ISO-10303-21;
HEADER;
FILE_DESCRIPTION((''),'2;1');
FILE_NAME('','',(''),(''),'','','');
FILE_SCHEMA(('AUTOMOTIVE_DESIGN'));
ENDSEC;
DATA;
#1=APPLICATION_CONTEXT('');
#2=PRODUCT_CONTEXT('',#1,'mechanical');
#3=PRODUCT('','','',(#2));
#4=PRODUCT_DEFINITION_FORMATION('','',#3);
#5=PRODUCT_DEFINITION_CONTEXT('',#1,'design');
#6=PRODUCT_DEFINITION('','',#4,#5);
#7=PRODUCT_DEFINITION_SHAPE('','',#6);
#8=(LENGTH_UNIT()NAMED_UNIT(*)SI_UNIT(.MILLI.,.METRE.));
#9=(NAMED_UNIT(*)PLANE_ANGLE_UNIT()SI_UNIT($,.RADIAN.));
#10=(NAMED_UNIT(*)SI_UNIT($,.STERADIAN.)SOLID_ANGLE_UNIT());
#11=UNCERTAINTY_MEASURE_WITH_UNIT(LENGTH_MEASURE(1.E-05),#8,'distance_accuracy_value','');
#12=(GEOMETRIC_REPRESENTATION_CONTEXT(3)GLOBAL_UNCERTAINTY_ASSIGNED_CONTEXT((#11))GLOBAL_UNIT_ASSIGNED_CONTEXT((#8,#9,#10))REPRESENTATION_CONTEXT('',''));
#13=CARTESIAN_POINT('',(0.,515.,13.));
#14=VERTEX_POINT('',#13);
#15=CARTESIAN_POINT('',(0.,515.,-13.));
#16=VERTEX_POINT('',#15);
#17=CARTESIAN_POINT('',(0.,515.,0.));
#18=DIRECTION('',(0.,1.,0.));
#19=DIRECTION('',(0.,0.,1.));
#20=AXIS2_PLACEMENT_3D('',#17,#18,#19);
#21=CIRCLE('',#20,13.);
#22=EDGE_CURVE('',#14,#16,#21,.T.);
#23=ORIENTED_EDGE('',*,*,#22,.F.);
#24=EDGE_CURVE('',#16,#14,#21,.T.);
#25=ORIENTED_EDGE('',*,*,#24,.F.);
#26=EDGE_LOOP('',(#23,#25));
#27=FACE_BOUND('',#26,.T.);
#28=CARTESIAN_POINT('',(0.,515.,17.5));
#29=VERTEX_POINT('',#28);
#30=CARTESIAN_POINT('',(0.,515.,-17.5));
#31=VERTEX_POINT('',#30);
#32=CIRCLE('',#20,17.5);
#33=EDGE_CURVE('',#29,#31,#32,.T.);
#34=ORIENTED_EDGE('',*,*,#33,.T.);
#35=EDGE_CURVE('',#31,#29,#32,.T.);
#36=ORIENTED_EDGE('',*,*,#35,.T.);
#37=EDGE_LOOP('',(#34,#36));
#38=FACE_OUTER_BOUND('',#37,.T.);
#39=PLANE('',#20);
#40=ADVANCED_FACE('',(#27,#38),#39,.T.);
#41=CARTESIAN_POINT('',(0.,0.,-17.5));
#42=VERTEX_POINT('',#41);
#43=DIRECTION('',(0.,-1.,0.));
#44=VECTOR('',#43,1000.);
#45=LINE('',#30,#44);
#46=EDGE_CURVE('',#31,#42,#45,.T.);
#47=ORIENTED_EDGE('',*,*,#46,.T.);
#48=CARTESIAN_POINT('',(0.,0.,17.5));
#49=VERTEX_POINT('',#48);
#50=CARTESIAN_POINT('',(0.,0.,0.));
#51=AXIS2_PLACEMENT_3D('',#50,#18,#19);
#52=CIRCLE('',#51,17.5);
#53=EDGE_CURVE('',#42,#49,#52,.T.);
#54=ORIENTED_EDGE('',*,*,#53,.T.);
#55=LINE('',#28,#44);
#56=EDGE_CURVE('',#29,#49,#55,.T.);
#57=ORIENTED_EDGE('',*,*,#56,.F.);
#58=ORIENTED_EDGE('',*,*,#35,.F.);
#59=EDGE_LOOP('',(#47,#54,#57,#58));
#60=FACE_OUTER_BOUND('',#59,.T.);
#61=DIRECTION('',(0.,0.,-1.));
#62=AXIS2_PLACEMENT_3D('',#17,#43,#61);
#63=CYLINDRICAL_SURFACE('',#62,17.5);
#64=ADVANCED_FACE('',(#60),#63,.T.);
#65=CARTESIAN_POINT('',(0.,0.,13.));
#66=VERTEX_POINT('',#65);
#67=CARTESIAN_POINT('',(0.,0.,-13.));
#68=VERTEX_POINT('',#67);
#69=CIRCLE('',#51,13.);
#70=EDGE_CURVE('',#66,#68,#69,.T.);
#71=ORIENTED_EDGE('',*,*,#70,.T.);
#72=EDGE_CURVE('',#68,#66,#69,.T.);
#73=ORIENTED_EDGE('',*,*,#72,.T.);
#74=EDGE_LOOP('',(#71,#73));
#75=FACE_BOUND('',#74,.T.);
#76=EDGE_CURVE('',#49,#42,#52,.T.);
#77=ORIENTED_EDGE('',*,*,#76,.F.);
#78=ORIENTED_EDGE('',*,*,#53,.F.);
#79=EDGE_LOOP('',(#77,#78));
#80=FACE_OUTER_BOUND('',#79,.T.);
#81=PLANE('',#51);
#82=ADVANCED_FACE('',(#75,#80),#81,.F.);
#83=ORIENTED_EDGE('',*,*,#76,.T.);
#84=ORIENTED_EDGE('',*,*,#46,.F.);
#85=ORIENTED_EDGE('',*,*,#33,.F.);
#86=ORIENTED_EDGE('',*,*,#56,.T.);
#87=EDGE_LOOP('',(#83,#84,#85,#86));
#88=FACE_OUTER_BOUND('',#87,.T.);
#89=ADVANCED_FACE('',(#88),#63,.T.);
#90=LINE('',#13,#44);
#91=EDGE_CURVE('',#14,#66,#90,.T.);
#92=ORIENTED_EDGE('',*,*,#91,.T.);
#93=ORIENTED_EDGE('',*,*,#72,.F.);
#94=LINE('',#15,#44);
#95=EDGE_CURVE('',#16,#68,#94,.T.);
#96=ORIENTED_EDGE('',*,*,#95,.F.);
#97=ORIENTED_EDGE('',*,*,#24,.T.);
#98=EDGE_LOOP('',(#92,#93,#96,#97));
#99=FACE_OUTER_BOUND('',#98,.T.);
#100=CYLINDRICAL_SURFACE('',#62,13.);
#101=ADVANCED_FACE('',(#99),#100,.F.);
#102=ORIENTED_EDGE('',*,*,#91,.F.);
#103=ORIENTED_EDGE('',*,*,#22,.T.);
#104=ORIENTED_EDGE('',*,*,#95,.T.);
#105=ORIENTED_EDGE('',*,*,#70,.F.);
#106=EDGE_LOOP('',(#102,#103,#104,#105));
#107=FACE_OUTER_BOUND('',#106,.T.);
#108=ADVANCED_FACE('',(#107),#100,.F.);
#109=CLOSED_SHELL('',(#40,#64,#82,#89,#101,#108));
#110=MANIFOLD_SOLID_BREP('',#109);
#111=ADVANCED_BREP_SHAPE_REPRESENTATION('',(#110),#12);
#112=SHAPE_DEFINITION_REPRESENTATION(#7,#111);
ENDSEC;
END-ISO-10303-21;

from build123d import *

# Parameters (mm, degrees)
SKETCH_1_R      = 17.5
EXTRUDE_1_DEPTH = 515
SHELL_1_T       = -4.5


with BuildPart() as part:
    # 草图1 → 凸台-拉伸1 (new body)
    with BuildSketch(Plane(origin=(0, 0, 0), x_dir=(1, 0, 0), z_dir=(0, 1, 0))):
        with Locations(Location((0, 0, 0), (0, 0, 270))):
            Circle(SKETCH_1_R)
    extrude(amount=EXTRUDE_1_DEPTH)

    # 抽壳1
    shell_1_openings = [part.faces().sort_by_distance(p)[0] for p in [
        (0, 515, 0),
        (0, 0, 0),
    ]]
    offset(amount=SHELL_1_T, openings=shell_1_openings, kind=Kind.INTERSECTION)


solid = part.part
